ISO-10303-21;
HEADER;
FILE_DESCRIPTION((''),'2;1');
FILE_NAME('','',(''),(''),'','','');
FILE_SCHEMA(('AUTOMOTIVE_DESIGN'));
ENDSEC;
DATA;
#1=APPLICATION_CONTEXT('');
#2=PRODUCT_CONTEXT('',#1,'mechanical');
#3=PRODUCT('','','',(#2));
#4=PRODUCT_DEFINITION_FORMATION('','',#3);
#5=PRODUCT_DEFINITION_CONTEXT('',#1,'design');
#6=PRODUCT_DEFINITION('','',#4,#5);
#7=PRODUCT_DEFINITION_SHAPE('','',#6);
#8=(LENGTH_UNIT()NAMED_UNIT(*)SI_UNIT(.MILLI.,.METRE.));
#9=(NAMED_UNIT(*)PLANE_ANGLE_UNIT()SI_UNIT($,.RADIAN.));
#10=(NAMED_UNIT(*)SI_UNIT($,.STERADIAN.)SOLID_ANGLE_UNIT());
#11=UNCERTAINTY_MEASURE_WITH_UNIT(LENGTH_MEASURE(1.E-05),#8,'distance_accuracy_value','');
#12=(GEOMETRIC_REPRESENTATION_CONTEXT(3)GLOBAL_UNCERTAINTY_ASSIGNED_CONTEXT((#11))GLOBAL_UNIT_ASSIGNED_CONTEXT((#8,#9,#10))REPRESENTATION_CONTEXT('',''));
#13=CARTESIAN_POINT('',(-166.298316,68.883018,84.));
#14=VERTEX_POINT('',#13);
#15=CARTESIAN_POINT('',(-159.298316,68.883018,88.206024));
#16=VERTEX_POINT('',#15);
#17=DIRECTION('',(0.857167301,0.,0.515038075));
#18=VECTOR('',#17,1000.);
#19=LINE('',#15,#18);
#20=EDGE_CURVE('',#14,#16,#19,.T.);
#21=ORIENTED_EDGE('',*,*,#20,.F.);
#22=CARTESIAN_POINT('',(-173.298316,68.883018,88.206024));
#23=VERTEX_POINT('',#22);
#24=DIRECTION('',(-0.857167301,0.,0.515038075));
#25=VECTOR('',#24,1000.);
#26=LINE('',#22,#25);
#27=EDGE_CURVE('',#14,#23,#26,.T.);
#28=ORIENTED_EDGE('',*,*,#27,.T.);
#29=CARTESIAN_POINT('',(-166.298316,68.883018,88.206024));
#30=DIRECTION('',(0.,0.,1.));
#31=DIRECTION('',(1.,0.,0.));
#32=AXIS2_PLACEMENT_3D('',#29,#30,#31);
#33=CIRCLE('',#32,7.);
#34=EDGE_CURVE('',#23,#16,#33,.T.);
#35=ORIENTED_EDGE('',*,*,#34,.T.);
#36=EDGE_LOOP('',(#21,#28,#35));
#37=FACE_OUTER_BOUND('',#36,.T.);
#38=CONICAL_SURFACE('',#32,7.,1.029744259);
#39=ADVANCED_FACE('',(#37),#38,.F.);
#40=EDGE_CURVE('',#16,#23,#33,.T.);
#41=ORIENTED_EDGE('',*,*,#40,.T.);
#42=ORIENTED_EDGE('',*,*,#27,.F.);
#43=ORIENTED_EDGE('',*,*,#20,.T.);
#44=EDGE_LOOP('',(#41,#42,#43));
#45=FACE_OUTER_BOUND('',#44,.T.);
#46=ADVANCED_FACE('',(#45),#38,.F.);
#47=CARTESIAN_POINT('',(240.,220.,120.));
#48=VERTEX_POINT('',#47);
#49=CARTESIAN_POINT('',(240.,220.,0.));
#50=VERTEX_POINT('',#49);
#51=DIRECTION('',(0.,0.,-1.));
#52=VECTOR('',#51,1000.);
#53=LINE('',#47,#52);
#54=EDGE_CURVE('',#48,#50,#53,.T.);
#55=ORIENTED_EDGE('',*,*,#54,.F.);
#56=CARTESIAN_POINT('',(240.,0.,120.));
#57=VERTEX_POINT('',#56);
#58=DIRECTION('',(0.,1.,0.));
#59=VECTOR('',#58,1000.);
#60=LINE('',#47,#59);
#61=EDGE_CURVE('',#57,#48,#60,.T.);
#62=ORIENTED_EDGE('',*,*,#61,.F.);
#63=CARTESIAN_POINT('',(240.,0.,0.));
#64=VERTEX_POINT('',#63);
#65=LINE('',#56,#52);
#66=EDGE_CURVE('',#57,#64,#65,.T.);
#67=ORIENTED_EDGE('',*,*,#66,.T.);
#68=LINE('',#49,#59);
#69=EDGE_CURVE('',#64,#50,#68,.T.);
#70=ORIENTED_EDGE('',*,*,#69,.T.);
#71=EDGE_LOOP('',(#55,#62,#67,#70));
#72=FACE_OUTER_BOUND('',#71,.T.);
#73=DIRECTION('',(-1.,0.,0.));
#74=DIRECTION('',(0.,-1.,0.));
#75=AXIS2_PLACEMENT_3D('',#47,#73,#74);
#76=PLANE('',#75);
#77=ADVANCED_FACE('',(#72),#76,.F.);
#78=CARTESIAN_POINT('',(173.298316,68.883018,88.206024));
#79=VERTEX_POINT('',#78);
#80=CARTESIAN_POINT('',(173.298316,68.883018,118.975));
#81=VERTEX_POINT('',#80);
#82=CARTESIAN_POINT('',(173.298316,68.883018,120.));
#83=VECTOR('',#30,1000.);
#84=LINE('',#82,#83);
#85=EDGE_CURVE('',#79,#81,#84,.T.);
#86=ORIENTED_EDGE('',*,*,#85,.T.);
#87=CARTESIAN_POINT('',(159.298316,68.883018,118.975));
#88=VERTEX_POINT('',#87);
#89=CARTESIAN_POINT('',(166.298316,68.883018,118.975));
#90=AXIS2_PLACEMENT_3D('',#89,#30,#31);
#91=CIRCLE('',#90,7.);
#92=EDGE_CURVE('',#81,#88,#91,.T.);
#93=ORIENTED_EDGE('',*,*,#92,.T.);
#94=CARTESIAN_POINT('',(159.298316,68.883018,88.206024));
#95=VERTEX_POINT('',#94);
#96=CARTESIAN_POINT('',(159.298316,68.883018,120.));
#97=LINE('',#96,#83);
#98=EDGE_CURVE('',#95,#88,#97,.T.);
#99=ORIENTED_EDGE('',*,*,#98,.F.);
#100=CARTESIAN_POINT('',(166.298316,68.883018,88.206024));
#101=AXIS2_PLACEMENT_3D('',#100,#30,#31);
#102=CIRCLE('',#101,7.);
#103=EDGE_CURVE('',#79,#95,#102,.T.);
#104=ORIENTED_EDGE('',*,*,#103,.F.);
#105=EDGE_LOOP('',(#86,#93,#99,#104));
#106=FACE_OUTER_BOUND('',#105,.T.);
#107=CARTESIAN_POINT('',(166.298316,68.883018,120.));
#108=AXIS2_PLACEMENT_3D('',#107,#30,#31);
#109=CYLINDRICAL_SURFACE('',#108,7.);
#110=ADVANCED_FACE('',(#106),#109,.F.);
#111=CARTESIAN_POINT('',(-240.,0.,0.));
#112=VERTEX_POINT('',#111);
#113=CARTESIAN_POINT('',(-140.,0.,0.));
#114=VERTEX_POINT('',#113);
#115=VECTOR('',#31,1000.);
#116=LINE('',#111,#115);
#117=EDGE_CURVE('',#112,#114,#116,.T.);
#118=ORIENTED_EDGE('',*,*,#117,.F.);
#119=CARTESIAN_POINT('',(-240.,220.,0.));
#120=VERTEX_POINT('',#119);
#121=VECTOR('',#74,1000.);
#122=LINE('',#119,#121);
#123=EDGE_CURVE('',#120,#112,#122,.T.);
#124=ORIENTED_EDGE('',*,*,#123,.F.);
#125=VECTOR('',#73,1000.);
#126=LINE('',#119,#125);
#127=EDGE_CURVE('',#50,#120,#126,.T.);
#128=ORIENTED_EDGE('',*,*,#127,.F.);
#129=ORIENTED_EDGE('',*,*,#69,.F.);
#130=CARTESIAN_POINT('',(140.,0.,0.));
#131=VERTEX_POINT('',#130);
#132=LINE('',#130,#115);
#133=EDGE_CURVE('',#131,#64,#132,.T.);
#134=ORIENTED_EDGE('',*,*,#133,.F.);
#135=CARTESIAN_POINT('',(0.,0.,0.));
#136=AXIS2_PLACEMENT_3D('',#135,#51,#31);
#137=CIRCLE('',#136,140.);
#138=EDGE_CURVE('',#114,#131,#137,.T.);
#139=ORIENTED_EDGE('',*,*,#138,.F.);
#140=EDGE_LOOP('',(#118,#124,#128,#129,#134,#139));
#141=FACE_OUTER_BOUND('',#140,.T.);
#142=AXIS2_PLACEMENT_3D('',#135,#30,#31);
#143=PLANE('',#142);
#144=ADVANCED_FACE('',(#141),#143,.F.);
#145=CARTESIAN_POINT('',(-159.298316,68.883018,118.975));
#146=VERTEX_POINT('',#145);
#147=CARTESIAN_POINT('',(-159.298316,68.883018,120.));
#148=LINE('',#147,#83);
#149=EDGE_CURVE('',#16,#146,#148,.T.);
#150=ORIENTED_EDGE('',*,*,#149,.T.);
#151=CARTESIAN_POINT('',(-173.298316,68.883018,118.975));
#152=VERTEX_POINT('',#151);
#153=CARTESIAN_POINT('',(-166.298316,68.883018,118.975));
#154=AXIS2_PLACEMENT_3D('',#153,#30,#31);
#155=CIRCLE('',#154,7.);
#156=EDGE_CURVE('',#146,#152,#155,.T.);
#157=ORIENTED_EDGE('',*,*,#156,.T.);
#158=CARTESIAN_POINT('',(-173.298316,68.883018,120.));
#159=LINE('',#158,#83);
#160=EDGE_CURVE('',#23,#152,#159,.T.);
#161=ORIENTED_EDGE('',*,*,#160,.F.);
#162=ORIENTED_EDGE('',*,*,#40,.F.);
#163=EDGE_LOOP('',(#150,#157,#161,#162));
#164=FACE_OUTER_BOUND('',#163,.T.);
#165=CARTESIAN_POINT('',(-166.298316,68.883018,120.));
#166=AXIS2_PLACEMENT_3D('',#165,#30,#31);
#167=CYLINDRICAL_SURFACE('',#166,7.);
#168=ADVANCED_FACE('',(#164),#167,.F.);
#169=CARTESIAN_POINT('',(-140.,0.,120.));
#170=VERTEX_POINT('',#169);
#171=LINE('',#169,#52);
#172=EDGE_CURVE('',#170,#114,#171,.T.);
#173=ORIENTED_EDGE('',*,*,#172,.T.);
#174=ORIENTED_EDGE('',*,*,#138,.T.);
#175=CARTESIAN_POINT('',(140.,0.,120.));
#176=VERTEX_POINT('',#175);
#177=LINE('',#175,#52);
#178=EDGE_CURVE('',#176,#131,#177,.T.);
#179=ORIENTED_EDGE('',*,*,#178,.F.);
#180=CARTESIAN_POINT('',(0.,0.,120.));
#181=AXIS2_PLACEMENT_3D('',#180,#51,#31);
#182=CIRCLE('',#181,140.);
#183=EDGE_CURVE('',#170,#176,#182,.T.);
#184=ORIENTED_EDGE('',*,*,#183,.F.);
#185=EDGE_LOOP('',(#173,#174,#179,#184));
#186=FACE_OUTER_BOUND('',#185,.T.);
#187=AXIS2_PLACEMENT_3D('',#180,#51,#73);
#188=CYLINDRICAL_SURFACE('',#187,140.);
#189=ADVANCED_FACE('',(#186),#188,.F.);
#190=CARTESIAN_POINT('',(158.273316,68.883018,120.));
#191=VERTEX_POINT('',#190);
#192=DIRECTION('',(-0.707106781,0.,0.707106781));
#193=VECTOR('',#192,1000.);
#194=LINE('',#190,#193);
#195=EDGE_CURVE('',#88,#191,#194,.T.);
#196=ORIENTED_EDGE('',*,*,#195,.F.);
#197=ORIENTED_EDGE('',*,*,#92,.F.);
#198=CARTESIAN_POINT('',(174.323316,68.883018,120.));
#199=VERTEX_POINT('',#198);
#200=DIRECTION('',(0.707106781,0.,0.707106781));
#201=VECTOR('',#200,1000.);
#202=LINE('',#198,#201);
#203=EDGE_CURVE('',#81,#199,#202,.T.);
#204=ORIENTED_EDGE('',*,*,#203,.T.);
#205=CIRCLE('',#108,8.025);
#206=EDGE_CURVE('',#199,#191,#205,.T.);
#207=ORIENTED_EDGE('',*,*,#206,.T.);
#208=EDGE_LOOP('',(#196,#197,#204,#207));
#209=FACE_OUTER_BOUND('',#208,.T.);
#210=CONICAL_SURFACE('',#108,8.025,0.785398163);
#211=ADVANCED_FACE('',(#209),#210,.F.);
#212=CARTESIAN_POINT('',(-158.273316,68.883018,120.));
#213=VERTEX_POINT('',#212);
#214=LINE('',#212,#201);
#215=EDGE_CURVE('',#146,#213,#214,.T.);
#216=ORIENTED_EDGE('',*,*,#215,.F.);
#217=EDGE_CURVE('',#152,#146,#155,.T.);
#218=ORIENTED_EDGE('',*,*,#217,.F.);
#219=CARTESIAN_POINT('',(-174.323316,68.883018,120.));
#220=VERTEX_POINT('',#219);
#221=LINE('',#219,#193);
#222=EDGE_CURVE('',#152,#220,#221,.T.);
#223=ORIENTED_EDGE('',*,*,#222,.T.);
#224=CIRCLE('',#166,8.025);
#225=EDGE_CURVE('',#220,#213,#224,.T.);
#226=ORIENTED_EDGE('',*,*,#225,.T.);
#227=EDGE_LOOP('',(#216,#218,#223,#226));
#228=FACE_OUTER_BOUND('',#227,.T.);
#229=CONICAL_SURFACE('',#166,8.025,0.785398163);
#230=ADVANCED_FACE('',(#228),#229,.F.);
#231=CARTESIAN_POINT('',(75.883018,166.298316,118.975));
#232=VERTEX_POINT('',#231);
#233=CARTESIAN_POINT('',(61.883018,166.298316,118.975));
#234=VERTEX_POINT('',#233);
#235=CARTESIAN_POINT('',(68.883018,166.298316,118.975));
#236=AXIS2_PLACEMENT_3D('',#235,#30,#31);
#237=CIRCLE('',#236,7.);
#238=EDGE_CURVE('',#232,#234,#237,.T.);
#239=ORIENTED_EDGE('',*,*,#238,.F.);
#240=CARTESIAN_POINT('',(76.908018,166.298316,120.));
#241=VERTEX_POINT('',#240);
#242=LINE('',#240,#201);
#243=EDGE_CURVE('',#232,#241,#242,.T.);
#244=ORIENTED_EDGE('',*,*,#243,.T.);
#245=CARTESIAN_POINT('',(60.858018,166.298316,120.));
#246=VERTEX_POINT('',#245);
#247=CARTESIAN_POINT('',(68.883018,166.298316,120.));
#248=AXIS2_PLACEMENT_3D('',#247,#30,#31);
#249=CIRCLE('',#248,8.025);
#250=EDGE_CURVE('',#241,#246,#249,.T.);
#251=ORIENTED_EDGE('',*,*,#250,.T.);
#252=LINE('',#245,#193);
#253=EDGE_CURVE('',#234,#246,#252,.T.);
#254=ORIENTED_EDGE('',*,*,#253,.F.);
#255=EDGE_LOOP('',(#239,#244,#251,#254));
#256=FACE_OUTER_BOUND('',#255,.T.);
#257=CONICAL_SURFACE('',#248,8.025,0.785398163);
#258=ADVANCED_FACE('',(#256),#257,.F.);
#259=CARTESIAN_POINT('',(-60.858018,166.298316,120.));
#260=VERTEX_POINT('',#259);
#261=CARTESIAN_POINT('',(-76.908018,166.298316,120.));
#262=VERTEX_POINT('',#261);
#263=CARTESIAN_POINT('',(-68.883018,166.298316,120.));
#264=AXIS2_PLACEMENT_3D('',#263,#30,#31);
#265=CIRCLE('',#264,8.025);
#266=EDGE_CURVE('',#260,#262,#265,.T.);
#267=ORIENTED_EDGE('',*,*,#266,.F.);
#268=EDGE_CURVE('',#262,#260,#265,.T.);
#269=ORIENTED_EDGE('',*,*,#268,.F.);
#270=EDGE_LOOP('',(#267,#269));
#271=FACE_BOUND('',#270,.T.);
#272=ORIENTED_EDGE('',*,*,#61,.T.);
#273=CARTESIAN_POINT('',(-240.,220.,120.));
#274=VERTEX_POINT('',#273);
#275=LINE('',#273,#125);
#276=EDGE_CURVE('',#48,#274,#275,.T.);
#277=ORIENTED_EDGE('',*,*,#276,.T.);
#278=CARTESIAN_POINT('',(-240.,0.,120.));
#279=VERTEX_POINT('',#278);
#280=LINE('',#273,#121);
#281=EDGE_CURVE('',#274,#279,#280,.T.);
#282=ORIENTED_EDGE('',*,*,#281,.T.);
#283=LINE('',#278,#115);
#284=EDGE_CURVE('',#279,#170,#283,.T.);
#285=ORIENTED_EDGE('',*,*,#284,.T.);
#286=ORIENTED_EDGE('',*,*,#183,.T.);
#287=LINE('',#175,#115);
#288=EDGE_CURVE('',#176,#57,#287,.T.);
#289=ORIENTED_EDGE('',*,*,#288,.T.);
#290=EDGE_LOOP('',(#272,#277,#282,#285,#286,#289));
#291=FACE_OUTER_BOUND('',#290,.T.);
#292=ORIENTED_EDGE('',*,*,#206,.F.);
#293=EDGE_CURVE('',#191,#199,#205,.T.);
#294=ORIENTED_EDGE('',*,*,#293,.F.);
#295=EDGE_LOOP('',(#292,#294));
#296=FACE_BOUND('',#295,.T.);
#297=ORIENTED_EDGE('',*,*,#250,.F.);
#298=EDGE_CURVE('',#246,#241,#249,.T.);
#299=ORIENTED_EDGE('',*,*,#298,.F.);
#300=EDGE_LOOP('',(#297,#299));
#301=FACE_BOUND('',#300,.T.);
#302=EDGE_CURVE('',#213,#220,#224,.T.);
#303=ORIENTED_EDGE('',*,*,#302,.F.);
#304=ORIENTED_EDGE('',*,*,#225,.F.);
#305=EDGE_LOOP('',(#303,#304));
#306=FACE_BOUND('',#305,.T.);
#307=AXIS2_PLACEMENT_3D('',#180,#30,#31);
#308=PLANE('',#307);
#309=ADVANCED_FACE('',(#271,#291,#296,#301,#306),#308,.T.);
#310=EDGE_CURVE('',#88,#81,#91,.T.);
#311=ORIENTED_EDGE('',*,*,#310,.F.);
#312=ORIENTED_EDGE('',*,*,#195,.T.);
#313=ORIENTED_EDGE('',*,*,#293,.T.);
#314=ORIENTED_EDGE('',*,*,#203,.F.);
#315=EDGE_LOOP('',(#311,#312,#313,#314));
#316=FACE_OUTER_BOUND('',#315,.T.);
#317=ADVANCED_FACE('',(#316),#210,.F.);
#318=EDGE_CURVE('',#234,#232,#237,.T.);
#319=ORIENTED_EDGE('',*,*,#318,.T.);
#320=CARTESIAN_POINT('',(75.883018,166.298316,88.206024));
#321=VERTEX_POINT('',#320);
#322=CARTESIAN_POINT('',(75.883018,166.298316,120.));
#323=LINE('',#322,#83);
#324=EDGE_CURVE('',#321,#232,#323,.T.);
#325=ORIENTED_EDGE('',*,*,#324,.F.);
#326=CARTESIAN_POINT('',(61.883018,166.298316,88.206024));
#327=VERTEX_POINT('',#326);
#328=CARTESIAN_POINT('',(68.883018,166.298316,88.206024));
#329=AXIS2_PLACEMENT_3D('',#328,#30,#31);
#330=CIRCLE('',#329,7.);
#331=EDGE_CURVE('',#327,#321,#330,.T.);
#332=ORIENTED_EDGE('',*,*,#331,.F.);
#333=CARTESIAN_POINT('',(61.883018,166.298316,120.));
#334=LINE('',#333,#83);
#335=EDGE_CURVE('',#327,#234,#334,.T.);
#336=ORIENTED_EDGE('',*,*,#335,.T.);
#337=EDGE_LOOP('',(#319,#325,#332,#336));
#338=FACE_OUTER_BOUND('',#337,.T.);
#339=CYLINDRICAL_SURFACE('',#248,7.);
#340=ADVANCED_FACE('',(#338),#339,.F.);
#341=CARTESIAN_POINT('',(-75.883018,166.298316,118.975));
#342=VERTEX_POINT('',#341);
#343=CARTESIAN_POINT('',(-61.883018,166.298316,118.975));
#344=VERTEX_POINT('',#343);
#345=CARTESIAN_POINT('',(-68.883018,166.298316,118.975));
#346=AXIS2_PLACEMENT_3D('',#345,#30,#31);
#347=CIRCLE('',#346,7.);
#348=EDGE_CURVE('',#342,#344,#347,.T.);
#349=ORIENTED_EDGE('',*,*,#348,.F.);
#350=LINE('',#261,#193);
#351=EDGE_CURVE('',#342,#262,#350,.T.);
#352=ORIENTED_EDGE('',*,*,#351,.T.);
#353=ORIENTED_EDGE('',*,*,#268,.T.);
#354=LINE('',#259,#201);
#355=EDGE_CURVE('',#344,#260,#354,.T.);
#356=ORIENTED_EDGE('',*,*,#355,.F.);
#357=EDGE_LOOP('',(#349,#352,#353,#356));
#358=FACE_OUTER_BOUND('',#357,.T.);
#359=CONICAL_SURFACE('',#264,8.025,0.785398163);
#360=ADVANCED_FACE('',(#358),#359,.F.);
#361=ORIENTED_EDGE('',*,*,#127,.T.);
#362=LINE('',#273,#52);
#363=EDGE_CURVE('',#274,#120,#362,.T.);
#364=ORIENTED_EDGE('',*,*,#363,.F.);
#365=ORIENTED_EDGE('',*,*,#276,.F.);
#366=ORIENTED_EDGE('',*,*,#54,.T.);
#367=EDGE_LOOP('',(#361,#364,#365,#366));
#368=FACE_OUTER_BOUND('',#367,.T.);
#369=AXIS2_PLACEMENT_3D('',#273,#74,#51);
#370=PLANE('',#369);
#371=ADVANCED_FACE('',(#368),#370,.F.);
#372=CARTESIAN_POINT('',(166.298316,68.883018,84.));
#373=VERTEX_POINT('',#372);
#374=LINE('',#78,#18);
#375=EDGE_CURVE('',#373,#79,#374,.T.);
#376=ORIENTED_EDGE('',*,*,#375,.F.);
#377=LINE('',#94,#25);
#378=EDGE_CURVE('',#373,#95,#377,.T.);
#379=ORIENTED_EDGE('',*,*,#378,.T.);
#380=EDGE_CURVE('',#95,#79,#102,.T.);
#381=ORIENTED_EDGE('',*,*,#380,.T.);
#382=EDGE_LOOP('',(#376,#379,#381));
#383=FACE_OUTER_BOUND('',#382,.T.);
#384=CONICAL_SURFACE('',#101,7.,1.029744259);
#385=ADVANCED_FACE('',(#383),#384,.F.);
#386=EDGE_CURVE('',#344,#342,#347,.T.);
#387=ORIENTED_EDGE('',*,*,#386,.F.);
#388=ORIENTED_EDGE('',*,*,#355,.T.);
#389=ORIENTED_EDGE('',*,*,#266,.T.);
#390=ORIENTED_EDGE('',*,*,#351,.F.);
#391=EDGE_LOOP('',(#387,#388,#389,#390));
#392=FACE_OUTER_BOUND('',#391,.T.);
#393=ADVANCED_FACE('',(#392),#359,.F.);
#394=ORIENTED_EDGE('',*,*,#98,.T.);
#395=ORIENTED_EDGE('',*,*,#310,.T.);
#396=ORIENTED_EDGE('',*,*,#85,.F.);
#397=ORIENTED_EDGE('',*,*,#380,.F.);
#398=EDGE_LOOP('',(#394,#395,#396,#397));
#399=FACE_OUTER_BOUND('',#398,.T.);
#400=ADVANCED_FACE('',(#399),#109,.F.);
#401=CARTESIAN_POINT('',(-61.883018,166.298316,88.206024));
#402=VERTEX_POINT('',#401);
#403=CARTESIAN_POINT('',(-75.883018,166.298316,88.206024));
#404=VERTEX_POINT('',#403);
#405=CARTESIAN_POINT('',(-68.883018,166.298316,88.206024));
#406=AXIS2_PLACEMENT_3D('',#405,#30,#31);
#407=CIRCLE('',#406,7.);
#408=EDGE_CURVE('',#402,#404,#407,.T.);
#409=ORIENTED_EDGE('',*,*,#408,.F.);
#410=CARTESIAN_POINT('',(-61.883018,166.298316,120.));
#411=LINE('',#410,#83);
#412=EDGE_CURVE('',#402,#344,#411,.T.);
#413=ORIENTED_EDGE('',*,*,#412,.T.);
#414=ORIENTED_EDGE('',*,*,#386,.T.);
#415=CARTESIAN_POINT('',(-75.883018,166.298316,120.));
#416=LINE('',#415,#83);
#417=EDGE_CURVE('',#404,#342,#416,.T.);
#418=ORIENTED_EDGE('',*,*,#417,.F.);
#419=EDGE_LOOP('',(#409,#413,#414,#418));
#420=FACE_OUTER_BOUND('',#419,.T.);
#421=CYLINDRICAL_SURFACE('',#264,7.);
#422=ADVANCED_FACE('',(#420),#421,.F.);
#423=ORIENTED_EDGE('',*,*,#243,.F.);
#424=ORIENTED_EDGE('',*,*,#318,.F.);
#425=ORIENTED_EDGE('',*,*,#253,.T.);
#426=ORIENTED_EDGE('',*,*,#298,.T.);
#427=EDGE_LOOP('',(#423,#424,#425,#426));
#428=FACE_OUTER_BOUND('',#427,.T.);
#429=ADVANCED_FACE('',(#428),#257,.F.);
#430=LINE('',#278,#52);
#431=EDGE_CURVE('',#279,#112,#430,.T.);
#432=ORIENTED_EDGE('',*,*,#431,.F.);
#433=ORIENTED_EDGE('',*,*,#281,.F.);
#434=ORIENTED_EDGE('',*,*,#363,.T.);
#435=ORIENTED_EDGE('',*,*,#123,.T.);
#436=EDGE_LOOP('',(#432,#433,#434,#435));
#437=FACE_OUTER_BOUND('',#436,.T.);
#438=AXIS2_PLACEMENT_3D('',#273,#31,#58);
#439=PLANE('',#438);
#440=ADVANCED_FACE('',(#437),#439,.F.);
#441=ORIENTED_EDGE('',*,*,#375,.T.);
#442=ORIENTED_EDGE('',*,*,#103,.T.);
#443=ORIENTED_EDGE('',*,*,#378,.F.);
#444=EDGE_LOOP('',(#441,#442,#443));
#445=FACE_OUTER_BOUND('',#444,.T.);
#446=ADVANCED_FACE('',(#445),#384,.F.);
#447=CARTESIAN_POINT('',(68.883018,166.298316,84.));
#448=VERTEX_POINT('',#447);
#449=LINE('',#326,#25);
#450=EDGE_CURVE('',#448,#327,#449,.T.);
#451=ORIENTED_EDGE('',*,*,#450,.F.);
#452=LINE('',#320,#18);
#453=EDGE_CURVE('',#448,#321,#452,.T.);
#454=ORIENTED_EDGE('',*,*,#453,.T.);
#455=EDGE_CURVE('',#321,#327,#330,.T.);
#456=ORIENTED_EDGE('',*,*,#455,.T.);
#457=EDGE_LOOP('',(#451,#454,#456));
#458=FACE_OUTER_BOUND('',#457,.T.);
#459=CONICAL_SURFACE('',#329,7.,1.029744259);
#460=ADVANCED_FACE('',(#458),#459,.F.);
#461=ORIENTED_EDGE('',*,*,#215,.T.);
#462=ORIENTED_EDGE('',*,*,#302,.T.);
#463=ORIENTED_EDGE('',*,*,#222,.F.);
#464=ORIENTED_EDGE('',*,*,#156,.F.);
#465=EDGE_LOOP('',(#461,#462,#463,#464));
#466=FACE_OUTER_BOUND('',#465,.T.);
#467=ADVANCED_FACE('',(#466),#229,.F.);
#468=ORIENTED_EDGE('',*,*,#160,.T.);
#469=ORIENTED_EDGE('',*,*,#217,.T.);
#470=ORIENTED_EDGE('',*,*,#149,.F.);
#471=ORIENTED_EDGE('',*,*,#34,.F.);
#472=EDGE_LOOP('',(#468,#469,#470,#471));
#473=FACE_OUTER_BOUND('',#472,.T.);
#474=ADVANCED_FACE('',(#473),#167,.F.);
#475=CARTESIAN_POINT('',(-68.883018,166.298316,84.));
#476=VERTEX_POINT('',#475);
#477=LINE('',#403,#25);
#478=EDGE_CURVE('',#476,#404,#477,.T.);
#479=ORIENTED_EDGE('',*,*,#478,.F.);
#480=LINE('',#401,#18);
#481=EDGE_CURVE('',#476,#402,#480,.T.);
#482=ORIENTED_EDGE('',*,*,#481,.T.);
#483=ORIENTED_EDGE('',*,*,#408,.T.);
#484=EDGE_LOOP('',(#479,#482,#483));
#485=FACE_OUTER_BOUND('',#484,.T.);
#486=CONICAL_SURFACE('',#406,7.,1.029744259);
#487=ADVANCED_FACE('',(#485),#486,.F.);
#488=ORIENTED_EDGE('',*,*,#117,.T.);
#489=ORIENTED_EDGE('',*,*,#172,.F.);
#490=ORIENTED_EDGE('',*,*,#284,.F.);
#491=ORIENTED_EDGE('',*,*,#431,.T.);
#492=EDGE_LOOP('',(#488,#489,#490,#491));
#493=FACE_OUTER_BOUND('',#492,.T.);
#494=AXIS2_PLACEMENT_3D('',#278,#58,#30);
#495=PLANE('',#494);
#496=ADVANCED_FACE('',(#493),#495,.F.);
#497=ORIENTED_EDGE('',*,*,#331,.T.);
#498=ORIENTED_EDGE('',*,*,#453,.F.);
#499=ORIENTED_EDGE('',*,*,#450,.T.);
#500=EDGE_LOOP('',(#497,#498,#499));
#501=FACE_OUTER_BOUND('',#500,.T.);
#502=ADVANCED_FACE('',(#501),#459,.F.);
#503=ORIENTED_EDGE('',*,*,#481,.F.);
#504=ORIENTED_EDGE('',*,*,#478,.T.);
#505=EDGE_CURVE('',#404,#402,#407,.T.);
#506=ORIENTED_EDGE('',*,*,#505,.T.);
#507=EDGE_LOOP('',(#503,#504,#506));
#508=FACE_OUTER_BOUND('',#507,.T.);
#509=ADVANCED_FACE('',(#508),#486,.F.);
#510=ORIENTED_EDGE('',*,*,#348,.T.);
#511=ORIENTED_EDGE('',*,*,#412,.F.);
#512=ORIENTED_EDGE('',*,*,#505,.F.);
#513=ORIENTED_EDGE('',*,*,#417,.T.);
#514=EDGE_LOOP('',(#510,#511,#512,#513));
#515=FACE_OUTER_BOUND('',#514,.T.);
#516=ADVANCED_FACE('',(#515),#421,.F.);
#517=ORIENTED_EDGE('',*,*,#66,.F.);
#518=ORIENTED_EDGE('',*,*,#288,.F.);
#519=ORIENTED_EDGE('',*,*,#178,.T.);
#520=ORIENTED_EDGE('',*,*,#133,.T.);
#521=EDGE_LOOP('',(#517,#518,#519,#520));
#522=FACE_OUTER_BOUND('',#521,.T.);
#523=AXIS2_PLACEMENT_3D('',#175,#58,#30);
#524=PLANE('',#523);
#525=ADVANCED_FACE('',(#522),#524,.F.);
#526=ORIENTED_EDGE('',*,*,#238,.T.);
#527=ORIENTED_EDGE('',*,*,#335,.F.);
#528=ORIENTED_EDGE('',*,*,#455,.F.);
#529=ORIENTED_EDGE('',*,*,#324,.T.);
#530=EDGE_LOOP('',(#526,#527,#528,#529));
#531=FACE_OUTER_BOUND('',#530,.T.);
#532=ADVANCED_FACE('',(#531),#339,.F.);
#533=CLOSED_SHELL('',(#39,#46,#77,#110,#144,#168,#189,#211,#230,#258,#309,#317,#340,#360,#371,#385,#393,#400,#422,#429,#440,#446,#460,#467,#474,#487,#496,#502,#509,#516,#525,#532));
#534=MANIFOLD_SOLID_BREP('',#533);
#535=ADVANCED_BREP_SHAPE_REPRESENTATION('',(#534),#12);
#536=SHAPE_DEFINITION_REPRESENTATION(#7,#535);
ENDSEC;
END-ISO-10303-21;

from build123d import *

# Parameters (mm, degrees)
BOSS_EXTRUDE1_DEPTH          = 120
M16_TAPPED_HOLE1_D           = 14
M16_TAPPED_HOLE1_DEPTH       = 31.793975667
M16_TAPPED_HOLE1_CSINK_D     = 16.05
M16_TAPPED_HOLE1_CSINK_ANGLE = 90
M16_TAPPED_HOLE1_TIP         = 4.206024333


with BuildPart() as part:
    # Sketch1 → Boss-Extrude1 (new body)
    with BuildSketch(Plane.XY):
        with BuildLine():
            Line((-240, 220), (240, 220))
            Line((240, 220), (240, 0))
            Line((240, 0), (140, 0))
            ThreePointArc((140, 0), (0, 140), (-140, 0))
            Line((-140, 0), (-240, 0))
            Line((-240, 0), (-240, 220))
        make_face()
    extrude(amount=BOSS_EXTRUDE1_DEPTH)

    # M16 Tapped Hole1
    with Locations(Plane.XY.offset(120)):
        with Locations((-166.298315852, 68.883017826), (-68.883017826, 166.298315852), (68.883017826, 166.298315852), (166.298315852, 68.883017826)):
            CounterSinkHole(M16_TAPPED_HOLE1_D / 2, M16_TAPPED_HOLE1_CSINK_D / 2, depth=M16_TAPPED_HOLE1_DEPTH, counter_sink_angle=M16_TAPPED_HOLE1_CSINK_ANGLE)
            with Locations((0, 0, -(M16_TAPPED_HOLE1_DEPTH + M16_TAPPED_HOLE1_TIP / 2))):  # 118° drill point
                Cone(0, M16_TAPPED_HOLE1_D / 2, M16_TAPPED_HOLE1_TIP, mode=Mode.SUBTRACT)


solid = part.part
